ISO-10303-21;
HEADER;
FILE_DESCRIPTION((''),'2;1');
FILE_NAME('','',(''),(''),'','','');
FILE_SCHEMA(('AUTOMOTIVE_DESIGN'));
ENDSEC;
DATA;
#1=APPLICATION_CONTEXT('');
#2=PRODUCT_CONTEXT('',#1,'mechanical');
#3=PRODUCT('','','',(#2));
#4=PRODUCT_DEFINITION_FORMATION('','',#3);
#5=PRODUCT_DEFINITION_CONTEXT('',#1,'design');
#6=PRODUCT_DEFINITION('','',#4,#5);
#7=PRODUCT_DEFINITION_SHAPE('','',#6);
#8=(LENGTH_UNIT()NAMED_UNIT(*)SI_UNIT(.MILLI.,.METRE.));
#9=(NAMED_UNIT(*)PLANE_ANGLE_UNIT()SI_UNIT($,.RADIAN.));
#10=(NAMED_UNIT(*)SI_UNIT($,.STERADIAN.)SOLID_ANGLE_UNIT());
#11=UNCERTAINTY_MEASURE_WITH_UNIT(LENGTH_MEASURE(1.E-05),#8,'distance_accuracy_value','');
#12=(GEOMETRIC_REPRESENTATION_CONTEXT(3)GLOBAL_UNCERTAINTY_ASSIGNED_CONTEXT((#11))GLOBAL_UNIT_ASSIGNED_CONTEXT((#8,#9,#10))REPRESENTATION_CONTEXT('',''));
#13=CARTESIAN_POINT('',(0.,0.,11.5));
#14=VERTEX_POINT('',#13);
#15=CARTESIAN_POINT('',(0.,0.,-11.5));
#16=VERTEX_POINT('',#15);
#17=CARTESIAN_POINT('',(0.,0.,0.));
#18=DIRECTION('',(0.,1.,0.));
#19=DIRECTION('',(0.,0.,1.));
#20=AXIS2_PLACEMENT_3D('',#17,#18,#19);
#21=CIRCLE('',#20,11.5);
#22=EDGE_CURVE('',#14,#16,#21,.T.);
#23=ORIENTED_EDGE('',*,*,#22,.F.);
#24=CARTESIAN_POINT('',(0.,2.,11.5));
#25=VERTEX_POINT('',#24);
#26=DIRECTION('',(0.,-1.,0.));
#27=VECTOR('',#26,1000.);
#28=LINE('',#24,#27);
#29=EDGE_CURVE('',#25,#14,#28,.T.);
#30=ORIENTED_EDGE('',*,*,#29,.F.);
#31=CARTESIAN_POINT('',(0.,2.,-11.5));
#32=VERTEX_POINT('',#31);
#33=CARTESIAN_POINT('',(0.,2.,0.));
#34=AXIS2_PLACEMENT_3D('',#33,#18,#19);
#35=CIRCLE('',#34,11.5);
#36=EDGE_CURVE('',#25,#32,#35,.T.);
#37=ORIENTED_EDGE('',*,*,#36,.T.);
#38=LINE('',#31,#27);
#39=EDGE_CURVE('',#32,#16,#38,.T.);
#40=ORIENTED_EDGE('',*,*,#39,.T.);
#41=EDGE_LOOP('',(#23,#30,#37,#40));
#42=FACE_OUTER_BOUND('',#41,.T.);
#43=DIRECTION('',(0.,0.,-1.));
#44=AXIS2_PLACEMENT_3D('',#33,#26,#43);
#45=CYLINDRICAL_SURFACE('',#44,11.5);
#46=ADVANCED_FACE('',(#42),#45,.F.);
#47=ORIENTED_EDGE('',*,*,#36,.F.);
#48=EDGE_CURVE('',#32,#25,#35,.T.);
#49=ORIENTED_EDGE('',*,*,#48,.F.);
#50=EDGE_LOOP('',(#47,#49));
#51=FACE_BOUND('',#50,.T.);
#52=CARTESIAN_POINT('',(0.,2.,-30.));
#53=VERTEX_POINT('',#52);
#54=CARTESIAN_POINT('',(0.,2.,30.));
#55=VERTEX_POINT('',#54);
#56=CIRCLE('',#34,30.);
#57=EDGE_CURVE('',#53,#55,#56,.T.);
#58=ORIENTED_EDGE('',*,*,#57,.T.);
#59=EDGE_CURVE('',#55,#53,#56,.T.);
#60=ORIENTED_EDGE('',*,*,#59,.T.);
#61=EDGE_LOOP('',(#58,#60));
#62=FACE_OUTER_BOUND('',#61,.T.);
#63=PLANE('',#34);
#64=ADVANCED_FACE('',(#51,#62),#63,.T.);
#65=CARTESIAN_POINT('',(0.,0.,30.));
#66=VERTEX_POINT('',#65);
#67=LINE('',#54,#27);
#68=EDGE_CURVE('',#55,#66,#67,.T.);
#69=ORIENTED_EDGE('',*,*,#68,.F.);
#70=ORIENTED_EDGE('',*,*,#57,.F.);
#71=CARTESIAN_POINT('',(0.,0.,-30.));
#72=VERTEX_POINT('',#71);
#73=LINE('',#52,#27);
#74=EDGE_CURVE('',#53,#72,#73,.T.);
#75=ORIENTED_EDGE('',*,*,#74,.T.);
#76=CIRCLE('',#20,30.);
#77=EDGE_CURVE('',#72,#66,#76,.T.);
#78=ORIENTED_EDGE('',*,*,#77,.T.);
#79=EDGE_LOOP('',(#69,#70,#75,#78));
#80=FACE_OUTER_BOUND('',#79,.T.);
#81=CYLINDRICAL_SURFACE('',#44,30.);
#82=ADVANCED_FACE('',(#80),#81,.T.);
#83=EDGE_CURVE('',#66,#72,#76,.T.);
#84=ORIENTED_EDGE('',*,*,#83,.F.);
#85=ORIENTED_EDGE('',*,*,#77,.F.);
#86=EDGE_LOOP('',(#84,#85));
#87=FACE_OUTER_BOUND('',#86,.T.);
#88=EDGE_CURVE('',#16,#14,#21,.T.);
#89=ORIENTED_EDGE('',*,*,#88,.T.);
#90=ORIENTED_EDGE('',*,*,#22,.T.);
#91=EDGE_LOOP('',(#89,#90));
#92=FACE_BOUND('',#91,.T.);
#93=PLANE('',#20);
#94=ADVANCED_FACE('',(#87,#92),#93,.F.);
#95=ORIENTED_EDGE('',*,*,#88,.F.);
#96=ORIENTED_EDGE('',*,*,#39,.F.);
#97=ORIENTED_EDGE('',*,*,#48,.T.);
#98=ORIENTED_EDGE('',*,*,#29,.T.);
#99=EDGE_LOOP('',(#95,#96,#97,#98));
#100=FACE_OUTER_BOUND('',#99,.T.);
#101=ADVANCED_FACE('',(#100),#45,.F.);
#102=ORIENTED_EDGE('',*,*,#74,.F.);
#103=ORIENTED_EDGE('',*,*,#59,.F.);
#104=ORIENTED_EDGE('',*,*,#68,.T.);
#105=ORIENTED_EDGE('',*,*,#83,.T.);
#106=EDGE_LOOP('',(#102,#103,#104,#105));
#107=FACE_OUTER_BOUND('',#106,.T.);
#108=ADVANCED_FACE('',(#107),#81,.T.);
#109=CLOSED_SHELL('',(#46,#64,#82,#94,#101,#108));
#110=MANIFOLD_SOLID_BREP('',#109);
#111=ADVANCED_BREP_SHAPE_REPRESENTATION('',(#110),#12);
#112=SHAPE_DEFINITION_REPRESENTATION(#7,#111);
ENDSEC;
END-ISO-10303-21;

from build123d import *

# Parameters (mm, degrees)
SKETCH1_R           = 30
SKETCH1_R_2         = 11.5
BOSS_EXTRUDE1_DEPTH = 2


with BuildPart() as part:
    # Sketch1 → Boss-Extrude1 (new body)
    with BuildSketch(Plane(origin=(0, 0, 0), x_dir=(1, 0, 0), z_dir=(0, 1, 0))):
        with Locations(Location((0, 0, 0), (0, 0, 270))):
            Circle(SKETCH1_R)
        with Locations(Location((0, 0, 0), (0, 0, 270))):
            Circle(SKETCH1_R_2, mode=Mode.SUBTRACT)
    extrude(amount=BOSS_EXTRUDE1_DEPTH)


solid = part.part
